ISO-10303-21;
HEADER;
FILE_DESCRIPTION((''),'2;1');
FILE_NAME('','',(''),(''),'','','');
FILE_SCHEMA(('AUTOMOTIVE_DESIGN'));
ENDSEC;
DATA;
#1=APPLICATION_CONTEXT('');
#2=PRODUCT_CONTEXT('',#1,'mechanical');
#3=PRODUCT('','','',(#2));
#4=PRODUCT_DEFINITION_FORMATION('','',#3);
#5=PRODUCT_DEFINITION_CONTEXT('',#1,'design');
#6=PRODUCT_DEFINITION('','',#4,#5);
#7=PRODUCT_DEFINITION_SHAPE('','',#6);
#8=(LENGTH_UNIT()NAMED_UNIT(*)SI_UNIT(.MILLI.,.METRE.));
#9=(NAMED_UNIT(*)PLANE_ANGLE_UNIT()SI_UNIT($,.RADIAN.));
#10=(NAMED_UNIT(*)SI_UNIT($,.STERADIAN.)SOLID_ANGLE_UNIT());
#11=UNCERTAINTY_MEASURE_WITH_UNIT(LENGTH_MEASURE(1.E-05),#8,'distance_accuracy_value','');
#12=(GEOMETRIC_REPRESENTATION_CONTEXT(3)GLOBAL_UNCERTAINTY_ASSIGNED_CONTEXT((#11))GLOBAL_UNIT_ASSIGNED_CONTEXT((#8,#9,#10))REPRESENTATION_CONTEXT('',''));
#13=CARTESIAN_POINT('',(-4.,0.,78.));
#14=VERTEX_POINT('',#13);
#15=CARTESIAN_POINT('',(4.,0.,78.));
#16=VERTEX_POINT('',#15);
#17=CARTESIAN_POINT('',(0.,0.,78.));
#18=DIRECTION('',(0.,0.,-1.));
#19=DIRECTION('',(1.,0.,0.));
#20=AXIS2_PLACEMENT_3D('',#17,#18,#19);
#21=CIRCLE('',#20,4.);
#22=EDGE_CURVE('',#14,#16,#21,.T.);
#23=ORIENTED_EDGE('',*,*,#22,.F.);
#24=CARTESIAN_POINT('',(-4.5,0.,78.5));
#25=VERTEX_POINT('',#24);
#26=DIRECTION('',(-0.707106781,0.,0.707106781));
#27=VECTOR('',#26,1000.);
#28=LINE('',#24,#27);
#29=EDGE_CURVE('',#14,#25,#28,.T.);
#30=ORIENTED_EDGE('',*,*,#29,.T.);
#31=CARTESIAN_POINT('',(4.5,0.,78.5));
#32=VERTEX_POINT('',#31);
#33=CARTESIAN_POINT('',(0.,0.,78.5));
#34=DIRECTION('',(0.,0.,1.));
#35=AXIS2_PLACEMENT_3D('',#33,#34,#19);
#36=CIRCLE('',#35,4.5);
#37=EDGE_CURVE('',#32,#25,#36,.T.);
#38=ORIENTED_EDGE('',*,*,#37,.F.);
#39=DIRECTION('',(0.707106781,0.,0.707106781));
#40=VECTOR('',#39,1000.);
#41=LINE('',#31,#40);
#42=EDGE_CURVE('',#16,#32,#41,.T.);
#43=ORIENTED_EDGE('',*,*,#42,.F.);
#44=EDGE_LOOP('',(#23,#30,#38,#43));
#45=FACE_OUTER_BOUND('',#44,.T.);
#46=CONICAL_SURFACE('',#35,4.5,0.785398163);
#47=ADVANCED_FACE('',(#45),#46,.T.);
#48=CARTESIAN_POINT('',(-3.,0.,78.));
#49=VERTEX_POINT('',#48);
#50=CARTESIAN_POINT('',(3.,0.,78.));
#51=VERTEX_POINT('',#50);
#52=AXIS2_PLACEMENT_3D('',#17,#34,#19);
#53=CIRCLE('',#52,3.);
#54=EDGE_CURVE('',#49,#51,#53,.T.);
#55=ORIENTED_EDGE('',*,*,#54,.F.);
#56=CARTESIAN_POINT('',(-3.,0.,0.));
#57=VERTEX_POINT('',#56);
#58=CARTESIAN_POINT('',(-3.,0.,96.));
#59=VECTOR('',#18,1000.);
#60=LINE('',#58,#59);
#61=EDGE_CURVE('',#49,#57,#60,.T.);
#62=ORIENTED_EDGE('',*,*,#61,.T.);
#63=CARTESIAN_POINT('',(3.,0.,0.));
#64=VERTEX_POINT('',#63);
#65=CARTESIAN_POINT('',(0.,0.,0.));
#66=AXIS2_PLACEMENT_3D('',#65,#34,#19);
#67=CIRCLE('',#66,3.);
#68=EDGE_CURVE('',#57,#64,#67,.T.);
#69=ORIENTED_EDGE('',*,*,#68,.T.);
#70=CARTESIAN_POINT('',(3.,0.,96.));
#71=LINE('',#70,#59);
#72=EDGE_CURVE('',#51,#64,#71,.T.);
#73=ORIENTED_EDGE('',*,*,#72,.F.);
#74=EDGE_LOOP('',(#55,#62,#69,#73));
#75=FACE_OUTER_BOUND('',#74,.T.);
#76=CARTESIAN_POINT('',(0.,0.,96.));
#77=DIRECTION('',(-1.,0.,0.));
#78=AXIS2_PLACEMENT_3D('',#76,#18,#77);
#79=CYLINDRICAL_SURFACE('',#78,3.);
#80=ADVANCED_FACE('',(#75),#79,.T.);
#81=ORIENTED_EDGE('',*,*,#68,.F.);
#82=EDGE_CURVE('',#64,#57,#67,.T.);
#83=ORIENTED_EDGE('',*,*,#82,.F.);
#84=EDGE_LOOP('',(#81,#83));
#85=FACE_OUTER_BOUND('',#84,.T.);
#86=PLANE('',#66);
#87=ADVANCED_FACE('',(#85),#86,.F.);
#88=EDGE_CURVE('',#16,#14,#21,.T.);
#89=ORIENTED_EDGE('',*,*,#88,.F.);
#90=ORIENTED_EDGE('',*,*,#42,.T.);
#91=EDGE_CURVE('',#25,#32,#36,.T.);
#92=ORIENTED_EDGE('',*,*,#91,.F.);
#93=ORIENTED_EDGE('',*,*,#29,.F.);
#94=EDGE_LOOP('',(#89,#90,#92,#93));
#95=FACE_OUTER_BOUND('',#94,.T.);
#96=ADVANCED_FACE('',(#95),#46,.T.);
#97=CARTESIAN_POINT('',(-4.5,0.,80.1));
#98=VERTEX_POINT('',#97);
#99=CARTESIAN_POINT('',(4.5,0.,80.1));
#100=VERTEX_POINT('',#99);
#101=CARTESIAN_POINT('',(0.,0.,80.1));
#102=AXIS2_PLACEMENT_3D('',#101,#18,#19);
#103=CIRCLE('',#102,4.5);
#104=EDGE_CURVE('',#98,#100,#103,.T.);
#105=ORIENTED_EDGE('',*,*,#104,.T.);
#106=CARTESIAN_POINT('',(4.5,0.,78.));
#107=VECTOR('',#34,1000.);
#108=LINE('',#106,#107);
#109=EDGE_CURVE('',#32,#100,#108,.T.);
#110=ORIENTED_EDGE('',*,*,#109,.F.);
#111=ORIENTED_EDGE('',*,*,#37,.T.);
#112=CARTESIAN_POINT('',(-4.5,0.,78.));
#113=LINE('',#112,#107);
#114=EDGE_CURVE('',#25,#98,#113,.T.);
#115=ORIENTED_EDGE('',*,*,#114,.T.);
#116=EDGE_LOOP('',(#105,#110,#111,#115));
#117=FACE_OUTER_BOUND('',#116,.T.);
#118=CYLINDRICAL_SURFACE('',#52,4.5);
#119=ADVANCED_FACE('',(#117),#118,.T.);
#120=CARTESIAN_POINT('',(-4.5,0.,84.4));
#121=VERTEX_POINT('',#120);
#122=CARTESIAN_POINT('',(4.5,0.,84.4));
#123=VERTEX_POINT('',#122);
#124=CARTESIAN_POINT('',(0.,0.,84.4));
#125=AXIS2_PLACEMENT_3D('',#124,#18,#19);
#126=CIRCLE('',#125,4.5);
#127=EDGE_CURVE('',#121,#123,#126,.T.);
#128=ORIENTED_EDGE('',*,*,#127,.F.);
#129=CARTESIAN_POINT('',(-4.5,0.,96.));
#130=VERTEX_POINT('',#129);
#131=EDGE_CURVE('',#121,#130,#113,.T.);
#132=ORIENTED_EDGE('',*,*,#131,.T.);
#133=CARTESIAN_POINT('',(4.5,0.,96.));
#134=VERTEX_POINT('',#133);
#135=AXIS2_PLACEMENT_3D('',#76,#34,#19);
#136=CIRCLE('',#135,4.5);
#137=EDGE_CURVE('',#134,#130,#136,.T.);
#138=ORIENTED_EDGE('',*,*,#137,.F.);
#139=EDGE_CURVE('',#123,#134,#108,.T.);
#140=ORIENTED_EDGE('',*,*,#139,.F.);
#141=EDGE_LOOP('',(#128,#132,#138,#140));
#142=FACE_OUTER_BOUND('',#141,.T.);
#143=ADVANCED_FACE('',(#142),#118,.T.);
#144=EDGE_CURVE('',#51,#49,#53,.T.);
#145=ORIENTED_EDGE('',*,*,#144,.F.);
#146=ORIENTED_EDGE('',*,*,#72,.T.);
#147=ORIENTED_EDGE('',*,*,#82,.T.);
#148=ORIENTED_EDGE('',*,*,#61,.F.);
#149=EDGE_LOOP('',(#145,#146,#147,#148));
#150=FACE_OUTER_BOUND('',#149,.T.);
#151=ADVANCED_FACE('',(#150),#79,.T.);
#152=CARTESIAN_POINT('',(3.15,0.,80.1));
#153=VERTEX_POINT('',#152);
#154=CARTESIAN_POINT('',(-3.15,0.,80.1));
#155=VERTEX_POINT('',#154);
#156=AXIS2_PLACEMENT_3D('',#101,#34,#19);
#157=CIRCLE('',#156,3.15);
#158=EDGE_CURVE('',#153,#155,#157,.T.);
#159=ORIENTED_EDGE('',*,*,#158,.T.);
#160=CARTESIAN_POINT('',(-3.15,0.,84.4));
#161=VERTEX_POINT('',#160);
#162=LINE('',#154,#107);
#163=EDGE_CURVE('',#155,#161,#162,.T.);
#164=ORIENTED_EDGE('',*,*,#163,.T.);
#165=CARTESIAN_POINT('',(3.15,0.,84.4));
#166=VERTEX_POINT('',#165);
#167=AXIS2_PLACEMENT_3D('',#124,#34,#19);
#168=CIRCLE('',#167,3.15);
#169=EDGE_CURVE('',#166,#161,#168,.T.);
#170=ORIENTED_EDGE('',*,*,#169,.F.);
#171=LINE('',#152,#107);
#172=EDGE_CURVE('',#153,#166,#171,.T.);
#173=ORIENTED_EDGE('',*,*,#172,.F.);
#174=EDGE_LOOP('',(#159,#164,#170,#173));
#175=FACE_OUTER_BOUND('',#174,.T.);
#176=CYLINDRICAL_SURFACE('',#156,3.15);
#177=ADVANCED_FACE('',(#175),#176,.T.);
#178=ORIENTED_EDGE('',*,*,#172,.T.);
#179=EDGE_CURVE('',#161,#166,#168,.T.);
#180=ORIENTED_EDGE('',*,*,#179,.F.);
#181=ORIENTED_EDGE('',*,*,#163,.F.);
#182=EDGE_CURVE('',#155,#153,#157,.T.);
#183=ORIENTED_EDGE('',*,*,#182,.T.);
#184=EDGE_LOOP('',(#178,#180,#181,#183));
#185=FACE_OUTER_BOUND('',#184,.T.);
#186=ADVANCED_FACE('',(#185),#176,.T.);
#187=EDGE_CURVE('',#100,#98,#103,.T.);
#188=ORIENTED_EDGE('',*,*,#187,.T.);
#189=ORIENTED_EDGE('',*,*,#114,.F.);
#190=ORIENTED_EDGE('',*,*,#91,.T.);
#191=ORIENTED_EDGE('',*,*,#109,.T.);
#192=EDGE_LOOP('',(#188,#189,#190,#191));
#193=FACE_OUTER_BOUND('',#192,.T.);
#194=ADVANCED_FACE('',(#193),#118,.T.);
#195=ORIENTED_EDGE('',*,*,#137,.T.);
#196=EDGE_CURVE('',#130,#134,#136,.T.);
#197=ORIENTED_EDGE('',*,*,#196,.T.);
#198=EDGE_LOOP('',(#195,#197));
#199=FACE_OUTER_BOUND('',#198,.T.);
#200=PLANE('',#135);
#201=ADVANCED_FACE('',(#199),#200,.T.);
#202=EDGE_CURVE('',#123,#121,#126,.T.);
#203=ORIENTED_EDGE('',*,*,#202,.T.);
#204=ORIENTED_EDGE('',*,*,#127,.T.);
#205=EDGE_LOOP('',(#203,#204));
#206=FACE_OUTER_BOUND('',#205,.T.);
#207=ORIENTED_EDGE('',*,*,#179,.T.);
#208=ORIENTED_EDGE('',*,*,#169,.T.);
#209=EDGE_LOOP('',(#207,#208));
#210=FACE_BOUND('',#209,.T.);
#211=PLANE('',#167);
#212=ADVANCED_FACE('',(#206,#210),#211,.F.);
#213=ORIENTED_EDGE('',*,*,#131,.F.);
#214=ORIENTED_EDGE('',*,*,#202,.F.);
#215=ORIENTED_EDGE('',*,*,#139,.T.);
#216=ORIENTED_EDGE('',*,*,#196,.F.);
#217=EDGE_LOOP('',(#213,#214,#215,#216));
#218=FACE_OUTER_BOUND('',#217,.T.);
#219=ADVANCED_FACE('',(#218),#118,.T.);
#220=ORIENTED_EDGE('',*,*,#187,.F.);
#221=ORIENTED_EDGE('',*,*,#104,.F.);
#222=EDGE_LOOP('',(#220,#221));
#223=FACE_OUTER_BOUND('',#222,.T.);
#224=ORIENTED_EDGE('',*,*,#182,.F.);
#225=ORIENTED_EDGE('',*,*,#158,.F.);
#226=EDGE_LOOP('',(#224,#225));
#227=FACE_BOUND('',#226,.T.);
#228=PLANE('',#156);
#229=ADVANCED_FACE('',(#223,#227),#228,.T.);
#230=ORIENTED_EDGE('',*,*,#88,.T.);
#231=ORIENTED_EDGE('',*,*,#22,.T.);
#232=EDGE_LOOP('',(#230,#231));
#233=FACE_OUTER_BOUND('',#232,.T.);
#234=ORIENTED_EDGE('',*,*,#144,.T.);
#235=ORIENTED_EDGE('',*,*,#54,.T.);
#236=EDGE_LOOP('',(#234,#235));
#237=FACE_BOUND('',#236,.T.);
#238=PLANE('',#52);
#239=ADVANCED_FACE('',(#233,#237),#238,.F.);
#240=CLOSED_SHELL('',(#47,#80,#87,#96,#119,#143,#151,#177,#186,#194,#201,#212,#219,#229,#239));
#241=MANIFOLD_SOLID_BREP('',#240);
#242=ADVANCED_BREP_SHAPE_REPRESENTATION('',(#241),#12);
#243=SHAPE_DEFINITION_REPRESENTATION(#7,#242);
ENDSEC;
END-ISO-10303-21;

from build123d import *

# Parameters (mm, degrees)
SKETCH1_R           = 3
BOSS_EXTRUDE1_DEPTH = 96
SKETCH2_R           = 4.5
BOSS_EXTRUDE2_DEPTH = 18
CUT_EXTRUDE1_START  = -11.6
SKETCH3_OUTSIDE_W   = 30.368
SKETCH3_OUTSIDE_H   = 30.368
SKETCH3_OUTSIDE_R   = 3.15
CUT_EXTRUDE1_DEPTH  = 4.3
CHAMFER1_SIZE       = 0.5


with BuildPart() as part:
    # Sketch1 → Boss-Extrude1 (new body)
    with BuildSketch(Plane.XY):
        Circle(SKETCH1_R)
    extrude(amount=BOSS_EXTRUDE1_DEPTH)

    # Sketch2 → Boss-Extrude2 (add)
    with BuildSketch(Plane.XY.offset(96)):
        Circle(SKETCH2_R)
    extrude(amount=-BOSS_EXTRUDE2_DEPTH)

    # Sketch3 outside → Cut-Extrude1 (cut)
    with BuildSketch(Plane.XY.offset(96).offset(CUT_EXTRUDE1_START)):
        Rectangle(SKETCH3_OUTSIDE_W, SKETCH3_OUTSIDE_H)
        Circle(SKETCH3_OUTSIDE_R, mode=Mode.SUBTRACT)
    extrude(amount=-CUT_EXTRUDE1_DEPTH, mode=Mode.SUBTRACT)

    # Chamfer1
    chamfer1_edges = [part.edges().sort_by_distance(p)[0] for p in [
        (-4.5, 0, 78),
    ]]
    chamfer(chamfer1_edges, length=CHAMFER1_SIZE)


solid = part.part
